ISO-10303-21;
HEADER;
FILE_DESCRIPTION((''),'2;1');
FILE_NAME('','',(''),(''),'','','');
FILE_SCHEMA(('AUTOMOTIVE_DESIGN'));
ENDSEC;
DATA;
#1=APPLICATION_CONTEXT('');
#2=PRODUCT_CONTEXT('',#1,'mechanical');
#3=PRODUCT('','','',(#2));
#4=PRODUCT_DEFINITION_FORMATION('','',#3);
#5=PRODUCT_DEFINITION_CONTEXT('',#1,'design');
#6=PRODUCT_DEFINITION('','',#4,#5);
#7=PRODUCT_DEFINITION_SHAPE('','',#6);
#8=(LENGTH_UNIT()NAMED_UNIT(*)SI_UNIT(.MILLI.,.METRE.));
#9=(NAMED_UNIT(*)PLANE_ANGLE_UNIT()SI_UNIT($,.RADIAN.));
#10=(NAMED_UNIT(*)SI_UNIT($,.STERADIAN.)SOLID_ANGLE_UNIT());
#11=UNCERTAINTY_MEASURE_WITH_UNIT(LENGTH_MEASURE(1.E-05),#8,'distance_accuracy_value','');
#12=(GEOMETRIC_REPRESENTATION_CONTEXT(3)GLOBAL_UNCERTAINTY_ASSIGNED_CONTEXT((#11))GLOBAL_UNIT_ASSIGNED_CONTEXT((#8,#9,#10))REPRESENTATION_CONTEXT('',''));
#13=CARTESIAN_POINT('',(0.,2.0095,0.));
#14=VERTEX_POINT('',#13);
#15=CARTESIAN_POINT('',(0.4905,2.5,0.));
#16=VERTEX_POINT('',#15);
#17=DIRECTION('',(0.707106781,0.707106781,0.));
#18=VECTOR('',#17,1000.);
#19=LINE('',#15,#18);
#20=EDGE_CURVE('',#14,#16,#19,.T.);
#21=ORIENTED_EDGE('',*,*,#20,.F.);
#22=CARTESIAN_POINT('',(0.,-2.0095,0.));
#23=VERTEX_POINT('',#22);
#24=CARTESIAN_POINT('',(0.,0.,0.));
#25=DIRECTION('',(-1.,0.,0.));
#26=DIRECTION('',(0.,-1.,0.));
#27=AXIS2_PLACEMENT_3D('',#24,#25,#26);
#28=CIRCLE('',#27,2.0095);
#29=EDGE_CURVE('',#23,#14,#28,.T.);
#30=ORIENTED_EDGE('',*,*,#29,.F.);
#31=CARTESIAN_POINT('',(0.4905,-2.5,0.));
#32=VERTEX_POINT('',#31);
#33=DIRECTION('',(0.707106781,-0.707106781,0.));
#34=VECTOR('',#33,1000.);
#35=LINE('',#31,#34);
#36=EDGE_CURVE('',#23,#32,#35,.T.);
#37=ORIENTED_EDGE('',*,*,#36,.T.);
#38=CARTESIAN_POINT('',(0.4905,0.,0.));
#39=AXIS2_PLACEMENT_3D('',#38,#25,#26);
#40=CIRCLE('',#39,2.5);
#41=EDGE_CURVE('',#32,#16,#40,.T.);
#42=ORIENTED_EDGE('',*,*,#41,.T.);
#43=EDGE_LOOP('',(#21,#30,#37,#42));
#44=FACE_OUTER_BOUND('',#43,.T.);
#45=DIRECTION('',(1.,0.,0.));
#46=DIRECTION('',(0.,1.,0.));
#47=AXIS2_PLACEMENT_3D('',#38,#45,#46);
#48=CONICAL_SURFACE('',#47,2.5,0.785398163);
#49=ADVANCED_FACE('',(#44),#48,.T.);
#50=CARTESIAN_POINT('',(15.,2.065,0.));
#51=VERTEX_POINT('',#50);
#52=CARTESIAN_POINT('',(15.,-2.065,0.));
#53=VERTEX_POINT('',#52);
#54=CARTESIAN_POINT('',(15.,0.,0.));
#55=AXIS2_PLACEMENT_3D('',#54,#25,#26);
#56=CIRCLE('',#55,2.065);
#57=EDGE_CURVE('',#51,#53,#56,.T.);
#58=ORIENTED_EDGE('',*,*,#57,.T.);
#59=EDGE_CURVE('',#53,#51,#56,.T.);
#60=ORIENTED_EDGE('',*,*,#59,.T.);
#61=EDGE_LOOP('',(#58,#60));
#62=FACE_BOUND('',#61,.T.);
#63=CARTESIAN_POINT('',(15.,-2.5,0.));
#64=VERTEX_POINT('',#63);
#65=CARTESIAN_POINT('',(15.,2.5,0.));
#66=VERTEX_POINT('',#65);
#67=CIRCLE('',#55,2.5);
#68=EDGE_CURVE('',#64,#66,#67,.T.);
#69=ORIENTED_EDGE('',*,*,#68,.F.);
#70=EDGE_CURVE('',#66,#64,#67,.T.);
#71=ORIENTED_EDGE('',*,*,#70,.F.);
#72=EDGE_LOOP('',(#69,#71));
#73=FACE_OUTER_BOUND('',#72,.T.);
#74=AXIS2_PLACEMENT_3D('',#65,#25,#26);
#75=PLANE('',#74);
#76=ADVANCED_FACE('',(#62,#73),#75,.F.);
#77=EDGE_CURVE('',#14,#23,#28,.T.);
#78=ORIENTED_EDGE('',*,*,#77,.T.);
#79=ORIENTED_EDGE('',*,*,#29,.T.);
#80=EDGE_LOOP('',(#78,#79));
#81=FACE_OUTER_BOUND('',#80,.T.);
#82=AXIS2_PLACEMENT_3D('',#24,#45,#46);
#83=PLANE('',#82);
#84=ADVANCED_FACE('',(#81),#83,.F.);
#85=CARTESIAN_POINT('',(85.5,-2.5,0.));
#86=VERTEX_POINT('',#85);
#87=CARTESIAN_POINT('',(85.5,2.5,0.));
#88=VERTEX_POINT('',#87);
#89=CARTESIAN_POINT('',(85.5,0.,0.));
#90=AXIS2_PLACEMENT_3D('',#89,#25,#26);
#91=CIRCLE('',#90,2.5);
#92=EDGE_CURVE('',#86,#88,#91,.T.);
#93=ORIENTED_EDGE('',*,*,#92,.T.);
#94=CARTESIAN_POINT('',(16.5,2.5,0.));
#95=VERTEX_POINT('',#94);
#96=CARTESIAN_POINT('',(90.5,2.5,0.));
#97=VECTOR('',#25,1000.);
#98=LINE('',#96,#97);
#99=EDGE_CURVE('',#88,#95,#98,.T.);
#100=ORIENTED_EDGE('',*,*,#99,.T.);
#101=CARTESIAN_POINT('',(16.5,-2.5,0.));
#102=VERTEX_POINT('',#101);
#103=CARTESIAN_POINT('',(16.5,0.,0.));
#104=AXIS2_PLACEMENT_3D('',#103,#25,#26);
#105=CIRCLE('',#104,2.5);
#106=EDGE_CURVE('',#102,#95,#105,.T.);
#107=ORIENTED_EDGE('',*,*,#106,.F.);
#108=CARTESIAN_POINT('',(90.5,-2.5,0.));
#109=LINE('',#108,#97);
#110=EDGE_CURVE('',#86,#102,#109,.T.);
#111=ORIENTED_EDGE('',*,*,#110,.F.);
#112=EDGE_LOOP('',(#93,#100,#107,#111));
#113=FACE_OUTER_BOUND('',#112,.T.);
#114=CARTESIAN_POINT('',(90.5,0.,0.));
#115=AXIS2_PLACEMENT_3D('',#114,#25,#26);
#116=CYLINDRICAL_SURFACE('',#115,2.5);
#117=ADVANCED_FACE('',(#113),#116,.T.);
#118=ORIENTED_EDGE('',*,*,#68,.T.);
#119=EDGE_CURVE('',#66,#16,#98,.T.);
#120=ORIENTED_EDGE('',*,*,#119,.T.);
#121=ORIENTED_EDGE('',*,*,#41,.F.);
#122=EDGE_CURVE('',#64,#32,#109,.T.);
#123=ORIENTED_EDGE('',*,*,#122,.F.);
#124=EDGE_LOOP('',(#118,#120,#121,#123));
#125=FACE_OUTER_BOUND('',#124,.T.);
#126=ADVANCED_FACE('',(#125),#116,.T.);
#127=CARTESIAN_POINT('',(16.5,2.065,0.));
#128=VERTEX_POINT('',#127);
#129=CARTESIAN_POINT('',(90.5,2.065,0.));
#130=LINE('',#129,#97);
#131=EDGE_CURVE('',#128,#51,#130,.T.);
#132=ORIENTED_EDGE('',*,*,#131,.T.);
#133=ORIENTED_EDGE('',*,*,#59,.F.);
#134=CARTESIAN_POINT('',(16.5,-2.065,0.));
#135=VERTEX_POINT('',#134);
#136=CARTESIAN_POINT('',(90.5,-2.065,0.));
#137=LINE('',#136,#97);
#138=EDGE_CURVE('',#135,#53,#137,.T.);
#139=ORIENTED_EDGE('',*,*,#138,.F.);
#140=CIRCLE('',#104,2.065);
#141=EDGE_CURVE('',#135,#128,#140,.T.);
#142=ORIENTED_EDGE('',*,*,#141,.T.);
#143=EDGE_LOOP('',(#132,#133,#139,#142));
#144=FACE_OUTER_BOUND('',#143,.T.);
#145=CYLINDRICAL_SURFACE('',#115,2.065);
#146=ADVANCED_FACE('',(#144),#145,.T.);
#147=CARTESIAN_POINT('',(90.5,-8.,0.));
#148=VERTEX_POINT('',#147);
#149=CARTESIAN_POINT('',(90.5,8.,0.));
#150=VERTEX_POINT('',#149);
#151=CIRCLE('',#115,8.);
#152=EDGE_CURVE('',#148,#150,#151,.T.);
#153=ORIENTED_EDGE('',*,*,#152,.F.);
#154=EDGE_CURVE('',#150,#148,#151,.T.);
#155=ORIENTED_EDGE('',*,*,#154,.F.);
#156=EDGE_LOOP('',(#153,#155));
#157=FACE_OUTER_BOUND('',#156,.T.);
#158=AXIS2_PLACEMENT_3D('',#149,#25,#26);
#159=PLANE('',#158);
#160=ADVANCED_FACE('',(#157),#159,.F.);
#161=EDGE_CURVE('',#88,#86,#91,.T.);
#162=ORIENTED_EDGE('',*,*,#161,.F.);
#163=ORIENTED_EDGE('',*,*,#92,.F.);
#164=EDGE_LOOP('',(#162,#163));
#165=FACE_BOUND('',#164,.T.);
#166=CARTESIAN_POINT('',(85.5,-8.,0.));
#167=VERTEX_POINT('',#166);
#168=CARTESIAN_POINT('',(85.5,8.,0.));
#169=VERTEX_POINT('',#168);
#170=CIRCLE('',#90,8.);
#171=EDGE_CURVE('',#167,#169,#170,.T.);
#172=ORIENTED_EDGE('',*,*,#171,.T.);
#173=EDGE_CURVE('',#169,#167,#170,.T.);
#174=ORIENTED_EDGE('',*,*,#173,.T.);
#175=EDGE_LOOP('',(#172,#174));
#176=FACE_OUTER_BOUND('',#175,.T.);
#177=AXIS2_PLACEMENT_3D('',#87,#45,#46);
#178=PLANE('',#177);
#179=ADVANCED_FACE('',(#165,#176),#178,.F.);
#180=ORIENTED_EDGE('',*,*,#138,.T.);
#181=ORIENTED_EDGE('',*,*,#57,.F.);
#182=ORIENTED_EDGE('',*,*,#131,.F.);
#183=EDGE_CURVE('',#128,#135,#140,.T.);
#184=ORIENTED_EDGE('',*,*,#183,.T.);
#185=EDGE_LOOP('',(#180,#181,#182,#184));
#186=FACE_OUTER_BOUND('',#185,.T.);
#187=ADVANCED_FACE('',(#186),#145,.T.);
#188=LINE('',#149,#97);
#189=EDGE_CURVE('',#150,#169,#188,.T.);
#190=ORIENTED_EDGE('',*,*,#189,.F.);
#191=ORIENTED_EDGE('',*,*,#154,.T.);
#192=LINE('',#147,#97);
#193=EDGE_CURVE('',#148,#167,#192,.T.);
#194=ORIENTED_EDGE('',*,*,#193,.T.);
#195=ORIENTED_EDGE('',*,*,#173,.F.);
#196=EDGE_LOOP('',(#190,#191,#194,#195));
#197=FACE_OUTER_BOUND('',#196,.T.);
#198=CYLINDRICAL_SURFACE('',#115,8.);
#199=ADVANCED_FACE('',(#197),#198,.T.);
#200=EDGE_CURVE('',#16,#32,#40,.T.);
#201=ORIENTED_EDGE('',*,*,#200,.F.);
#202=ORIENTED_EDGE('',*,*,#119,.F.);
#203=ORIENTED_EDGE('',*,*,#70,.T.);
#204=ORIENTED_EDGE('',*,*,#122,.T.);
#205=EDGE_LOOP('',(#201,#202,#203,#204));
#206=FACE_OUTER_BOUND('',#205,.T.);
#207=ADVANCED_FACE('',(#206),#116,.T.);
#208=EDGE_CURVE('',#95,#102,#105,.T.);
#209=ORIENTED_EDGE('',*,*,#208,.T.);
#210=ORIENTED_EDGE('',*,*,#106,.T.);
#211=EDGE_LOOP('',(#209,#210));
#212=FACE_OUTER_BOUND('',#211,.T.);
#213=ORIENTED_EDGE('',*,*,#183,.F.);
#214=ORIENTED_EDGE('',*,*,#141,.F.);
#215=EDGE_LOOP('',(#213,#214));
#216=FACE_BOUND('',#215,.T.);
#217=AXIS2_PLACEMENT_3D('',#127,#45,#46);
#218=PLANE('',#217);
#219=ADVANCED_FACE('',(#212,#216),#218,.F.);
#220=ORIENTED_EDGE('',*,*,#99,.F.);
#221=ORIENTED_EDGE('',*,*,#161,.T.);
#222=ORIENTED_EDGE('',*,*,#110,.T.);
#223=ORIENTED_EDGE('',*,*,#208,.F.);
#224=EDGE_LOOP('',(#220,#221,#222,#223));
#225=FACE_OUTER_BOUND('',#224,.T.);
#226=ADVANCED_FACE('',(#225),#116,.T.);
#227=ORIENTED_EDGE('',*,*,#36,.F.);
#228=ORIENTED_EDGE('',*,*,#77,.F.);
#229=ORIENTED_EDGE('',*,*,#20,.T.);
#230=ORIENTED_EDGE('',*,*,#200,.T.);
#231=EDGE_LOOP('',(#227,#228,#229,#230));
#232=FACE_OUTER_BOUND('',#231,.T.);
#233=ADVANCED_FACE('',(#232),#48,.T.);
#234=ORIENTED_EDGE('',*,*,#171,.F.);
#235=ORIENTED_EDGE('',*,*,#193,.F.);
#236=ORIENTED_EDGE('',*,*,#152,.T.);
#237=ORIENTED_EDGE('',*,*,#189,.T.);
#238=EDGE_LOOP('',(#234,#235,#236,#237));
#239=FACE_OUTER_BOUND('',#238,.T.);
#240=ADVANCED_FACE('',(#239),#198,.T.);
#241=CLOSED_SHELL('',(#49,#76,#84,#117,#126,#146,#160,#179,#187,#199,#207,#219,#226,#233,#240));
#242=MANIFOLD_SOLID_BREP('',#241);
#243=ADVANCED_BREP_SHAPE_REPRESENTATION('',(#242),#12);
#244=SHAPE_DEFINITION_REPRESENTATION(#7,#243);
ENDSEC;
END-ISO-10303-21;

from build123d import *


with BuildPart() as part:
    # Sketch1 → Revolve1 (revolve)
    with BuildSketch(Plane.XY, mode=Mode.PRIVATE) as revolve1_sk:
        Polygon((0, 0), (0, 2.0095), (0.4905, 2.5), (15, 2.5), (15, 2.065), (16.5, 2.065), (16.5, 2.5), (85.5, 2.5), (85.5, 8), (90.5, 8), (90.5, 0), align=None)
    revolve(revolve1_sk.sketch.rotate(Axis((90.5, 0, 0), (-1, 0, 0)), 180), axis=Axis((90.5, 0, 0), (-1, 0, 0)))


solid = part.part
